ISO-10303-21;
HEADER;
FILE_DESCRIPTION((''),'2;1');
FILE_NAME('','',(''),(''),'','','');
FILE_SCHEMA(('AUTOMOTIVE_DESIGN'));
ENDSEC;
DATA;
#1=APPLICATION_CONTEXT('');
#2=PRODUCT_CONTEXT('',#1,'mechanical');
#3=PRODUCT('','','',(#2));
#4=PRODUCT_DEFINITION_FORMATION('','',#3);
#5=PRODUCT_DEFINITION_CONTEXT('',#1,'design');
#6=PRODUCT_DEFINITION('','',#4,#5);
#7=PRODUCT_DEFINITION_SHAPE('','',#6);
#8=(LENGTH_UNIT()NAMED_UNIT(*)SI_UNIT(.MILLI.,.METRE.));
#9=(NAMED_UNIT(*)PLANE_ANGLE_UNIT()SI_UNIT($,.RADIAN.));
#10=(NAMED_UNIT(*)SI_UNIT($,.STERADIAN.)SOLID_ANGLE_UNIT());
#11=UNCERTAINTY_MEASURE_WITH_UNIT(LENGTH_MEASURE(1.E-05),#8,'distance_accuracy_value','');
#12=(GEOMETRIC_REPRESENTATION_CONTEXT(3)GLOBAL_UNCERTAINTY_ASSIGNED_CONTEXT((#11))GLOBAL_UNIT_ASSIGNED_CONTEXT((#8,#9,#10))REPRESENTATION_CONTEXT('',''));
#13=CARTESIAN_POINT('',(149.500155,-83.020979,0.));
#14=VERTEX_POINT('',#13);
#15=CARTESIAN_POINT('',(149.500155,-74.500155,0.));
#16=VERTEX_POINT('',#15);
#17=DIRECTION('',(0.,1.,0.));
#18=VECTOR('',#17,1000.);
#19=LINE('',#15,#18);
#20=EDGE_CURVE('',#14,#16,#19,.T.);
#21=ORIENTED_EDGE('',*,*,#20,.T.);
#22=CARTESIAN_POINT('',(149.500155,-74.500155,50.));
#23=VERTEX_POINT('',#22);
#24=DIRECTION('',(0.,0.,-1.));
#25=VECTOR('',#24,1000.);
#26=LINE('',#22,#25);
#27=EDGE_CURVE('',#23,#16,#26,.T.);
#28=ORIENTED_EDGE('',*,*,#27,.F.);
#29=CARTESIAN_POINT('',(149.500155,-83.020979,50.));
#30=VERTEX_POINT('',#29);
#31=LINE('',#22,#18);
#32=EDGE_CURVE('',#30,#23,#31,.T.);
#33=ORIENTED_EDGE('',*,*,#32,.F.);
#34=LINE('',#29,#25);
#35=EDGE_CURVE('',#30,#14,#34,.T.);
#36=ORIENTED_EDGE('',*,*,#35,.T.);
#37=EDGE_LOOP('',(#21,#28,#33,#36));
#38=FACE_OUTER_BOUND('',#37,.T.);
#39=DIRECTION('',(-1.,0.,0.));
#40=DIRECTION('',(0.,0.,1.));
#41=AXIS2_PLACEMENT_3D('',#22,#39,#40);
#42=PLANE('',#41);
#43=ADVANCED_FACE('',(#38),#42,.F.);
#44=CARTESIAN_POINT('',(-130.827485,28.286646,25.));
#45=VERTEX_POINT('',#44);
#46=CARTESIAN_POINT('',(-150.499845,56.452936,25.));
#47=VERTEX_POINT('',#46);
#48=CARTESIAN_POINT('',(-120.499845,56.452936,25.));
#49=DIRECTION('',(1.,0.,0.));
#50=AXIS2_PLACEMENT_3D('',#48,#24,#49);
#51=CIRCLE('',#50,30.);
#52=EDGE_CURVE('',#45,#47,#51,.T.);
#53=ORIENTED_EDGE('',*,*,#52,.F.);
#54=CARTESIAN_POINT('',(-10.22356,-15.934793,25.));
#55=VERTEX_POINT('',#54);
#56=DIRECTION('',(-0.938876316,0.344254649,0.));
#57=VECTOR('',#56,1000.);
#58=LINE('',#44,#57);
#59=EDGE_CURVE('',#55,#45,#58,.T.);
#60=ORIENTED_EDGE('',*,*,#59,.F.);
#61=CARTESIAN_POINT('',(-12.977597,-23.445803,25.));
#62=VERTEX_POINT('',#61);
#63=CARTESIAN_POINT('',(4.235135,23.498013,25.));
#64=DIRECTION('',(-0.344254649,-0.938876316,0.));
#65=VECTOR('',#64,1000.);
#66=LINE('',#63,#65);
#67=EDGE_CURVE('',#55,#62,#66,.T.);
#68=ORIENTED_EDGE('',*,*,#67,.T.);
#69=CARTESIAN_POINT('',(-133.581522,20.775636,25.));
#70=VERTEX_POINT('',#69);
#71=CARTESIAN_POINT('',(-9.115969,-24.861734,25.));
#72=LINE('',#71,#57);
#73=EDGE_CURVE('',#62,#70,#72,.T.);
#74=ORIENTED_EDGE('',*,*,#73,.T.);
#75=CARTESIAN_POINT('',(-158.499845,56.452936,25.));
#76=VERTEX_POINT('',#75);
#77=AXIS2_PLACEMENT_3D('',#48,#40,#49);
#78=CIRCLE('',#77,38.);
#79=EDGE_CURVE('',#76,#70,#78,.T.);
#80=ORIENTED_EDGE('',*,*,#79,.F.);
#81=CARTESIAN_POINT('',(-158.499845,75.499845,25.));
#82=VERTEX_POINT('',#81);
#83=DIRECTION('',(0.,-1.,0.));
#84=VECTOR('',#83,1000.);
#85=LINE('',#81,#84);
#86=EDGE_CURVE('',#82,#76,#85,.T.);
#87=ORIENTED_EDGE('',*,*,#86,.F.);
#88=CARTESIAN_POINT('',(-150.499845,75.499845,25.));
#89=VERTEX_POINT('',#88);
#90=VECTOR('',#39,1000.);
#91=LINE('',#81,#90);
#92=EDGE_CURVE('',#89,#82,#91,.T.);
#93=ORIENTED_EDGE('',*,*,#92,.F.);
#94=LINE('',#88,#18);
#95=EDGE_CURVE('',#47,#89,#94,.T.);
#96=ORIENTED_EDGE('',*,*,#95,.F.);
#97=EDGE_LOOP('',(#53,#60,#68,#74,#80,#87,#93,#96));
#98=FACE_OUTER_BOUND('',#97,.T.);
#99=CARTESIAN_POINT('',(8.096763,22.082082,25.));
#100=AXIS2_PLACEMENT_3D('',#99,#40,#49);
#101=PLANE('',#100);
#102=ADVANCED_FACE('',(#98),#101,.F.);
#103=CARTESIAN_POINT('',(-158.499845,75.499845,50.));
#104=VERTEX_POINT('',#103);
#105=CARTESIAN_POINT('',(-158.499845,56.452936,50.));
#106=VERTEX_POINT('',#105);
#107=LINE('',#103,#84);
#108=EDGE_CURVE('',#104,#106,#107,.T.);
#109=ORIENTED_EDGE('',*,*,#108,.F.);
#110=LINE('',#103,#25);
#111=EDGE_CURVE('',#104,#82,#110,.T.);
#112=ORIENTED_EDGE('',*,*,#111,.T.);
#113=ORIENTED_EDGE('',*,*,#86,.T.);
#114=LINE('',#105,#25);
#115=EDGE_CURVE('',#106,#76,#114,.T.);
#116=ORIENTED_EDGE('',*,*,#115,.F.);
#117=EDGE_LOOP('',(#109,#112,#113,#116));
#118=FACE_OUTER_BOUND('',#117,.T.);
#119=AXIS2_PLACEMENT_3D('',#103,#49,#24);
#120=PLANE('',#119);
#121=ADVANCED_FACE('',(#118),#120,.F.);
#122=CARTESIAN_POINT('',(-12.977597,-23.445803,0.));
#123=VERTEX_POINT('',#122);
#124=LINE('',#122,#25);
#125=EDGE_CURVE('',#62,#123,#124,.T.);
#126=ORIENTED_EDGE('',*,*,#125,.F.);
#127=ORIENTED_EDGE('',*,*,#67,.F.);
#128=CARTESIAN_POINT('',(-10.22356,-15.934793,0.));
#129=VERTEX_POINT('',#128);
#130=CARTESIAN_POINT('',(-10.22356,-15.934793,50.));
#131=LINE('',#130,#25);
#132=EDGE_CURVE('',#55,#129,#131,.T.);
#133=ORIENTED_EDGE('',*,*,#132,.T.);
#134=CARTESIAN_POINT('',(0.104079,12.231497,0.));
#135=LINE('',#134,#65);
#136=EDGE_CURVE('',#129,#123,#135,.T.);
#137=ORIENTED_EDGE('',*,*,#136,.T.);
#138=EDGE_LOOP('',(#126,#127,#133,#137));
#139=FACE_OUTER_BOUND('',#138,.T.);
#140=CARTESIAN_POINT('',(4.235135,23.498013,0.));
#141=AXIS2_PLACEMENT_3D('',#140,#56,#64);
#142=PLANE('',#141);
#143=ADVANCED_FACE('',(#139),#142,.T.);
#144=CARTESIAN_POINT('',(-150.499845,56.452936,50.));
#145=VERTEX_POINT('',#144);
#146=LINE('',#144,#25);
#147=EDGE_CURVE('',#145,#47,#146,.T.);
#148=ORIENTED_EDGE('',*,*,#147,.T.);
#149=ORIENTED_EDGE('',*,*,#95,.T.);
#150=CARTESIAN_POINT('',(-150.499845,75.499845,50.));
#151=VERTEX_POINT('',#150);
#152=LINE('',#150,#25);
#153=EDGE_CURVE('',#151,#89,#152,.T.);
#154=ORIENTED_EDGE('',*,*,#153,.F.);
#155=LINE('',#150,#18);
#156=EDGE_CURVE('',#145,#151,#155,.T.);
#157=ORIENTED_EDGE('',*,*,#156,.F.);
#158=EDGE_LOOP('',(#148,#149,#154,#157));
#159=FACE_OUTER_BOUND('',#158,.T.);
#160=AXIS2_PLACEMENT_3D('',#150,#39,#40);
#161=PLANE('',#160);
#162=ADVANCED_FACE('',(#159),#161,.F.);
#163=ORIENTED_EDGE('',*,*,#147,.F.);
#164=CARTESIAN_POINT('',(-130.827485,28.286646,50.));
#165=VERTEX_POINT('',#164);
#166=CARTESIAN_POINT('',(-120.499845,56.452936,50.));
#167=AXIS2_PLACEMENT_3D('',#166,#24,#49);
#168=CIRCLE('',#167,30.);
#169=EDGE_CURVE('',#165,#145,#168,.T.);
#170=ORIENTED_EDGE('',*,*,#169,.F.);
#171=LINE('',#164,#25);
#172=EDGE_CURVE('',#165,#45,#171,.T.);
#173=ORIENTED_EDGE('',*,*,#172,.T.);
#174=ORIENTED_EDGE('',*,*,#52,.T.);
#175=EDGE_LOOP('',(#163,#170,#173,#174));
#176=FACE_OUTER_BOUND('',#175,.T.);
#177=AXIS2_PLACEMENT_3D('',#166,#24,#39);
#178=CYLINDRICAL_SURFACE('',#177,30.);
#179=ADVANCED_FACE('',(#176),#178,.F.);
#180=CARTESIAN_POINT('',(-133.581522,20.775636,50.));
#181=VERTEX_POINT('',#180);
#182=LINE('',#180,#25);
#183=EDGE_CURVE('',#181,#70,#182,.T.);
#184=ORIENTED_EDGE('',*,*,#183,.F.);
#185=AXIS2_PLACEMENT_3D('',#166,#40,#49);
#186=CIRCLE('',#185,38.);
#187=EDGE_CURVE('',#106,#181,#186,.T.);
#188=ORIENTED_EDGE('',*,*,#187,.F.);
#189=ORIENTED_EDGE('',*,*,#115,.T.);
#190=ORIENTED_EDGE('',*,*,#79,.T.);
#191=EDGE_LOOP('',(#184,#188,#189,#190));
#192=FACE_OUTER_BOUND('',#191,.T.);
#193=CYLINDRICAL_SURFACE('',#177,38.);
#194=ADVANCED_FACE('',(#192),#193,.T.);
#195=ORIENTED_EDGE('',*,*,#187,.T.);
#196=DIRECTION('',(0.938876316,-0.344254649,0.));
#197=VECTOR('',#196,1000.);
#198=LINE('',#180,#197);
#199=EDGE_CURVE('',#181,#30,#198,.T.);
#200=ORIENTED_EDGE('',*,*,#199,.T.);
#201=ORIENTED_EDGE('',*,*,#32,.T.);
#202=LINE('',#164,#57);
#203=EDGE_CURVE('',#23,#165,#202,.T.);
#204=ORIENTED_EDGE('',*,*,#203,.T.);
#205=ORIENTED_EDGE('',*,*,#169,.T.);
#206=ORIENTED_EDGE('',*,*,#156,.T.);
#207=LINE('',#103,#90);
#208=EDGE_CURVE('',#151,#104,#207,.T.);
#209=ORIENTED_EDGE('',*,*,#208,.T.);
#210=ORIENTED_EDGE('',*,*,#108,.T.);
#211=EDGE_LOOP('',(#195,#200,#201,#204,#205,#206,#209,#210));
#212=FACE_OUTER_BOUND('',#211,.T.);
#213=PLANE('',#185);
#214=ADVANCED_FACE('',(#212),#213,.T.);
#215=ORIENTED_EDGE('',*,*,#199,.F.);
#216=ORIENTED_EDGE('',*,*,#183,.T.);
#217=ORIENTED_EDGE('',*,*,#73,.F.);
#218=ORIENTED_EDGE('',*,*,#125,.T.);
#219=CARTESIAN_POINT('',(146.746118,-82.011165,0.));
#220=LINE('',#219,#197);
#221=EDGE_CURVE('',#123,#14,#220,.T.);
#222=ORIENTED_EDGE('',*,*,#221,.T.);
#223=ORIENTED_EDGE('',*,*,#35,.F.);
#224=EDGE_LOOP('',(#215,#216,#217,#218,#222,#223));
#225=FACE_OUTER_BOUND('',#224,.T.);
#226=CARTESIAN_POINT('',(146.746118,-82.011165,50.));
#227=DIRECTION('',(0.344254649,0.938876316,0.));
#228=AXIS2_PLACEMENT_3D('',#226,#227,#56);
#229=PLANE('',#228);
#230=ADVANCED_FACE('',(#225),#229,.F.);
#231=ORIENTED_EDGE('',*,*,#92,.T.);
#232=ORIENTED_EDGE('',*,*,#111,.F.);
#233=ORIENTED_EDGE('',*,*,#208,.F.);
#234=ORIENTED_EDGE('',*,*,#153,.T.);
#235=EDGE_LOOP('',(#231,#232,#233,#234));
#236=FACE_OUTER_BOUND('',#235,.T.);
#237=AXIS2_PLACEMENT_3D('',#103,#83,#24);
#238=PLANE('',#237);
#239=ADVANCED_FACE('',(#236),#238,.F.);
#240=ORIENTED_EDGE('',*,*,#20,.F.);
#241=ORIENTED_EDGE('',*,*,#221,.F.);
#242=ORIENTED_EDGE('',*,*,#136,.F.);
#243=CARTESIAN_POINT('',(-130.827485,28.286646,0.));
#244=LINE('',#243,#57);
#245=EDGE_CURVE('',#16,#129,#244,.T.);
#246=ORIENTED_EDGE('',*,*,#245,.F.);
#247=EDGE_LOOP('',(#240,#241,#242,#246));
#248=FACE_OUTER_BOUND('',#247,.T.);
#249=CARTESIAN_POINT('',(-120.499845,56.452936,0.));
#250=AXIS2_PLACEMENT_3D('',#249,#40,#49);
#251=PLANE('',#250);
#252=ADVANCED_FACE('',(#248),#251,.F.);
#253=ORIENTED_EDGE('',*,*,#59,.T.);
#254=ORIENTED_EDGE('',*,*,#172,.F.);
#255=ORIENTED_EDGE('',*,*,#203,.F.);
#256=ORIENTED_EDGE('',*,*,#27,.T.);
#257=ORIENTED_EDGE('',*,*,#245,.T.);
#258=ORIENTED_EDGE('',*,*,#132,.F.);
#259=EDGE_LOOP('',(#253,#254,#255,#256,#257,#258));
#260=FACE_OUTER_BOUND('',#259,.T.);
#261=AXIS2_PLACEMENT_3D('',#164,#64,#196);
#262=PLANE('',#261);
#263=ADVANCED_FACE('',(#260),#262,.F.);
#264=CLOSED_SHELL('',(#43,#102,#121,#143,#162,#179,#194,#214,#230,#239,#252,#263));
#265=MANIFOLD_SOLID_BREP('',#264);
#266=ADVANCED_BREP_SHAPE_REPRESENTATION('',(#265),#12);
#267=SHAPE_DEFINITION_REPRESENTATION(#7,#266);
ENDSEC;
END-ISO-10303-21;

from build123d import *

# Parameters (mm, degrees)
EXTRUDE_1_DEPTH     = 50
SKETCH_2_W          = 128.455604429
SKETCH_2_H          = 25
SKETCH_2_W_2        = 42.23428711
CUT_EXTRUDE_2_DEPTH = 50


with BuildPart() as part:
    # 草图1 → 凸台-拉伸1 (new body)
    with BuildSketch(Plane.XY):
        with BuildLine():
            Line((-158.499845276, 75.499845276), (-158.499845276, 56.452935893))
            ThreePointArc((-158.499845276, 56.452935893), (-151.653526546, 34.694072336), (-133.581521944, 20.77563589))
            Line((-133.581521944, 20.77563589), (146.746117531, -82.011165251))
            Line((146.746117531, -82.011165251), (149.500154724, -83.020978889))
            Line((149.500154724, -83.020978889), (149.500154724, -74.500154724))
            Line((149.500154724, -74.500154724), (-130.827484751, 28.286646417))
            ThreePointArc((-130.827484751, 28.286646417), (-145.094856805, 39.274885717), (-150.499845276, 56.452935893))
            Line((-150.499845276, 56.452935893), (-150.499845276, 75.499845276))
            Line((-150.499845276, 75.499845276), (-158.499845276, 75.499845276))
        make_face()
    extrude(amount=EXTRUDE_1_DEPTH)

    # 草图2 → 切除-拉伸2 (cut)
    with BuildSketch(Plane(origin=(-9.115968963, -24.861733537, 0), x_dir=(0.9388763158866098, -0.3442546491584201, 0), z_dir=(-0.3442546491584201, -0.9388763158866098, 0))):
        with Locations((-68.340834223, 12.5)):
            Rectangle(SKETCH_2_W, SKETCH_2_H)
        with Locations((-153.685779993, 12.5)):
            Rectangle(SKETCH_2_W_2, SKETCH_2_H)
    extrude(amount=-CUT_EXTRUDE_2_DEPTH, mode=Mode.SUBTRACT)


solid = part.part
